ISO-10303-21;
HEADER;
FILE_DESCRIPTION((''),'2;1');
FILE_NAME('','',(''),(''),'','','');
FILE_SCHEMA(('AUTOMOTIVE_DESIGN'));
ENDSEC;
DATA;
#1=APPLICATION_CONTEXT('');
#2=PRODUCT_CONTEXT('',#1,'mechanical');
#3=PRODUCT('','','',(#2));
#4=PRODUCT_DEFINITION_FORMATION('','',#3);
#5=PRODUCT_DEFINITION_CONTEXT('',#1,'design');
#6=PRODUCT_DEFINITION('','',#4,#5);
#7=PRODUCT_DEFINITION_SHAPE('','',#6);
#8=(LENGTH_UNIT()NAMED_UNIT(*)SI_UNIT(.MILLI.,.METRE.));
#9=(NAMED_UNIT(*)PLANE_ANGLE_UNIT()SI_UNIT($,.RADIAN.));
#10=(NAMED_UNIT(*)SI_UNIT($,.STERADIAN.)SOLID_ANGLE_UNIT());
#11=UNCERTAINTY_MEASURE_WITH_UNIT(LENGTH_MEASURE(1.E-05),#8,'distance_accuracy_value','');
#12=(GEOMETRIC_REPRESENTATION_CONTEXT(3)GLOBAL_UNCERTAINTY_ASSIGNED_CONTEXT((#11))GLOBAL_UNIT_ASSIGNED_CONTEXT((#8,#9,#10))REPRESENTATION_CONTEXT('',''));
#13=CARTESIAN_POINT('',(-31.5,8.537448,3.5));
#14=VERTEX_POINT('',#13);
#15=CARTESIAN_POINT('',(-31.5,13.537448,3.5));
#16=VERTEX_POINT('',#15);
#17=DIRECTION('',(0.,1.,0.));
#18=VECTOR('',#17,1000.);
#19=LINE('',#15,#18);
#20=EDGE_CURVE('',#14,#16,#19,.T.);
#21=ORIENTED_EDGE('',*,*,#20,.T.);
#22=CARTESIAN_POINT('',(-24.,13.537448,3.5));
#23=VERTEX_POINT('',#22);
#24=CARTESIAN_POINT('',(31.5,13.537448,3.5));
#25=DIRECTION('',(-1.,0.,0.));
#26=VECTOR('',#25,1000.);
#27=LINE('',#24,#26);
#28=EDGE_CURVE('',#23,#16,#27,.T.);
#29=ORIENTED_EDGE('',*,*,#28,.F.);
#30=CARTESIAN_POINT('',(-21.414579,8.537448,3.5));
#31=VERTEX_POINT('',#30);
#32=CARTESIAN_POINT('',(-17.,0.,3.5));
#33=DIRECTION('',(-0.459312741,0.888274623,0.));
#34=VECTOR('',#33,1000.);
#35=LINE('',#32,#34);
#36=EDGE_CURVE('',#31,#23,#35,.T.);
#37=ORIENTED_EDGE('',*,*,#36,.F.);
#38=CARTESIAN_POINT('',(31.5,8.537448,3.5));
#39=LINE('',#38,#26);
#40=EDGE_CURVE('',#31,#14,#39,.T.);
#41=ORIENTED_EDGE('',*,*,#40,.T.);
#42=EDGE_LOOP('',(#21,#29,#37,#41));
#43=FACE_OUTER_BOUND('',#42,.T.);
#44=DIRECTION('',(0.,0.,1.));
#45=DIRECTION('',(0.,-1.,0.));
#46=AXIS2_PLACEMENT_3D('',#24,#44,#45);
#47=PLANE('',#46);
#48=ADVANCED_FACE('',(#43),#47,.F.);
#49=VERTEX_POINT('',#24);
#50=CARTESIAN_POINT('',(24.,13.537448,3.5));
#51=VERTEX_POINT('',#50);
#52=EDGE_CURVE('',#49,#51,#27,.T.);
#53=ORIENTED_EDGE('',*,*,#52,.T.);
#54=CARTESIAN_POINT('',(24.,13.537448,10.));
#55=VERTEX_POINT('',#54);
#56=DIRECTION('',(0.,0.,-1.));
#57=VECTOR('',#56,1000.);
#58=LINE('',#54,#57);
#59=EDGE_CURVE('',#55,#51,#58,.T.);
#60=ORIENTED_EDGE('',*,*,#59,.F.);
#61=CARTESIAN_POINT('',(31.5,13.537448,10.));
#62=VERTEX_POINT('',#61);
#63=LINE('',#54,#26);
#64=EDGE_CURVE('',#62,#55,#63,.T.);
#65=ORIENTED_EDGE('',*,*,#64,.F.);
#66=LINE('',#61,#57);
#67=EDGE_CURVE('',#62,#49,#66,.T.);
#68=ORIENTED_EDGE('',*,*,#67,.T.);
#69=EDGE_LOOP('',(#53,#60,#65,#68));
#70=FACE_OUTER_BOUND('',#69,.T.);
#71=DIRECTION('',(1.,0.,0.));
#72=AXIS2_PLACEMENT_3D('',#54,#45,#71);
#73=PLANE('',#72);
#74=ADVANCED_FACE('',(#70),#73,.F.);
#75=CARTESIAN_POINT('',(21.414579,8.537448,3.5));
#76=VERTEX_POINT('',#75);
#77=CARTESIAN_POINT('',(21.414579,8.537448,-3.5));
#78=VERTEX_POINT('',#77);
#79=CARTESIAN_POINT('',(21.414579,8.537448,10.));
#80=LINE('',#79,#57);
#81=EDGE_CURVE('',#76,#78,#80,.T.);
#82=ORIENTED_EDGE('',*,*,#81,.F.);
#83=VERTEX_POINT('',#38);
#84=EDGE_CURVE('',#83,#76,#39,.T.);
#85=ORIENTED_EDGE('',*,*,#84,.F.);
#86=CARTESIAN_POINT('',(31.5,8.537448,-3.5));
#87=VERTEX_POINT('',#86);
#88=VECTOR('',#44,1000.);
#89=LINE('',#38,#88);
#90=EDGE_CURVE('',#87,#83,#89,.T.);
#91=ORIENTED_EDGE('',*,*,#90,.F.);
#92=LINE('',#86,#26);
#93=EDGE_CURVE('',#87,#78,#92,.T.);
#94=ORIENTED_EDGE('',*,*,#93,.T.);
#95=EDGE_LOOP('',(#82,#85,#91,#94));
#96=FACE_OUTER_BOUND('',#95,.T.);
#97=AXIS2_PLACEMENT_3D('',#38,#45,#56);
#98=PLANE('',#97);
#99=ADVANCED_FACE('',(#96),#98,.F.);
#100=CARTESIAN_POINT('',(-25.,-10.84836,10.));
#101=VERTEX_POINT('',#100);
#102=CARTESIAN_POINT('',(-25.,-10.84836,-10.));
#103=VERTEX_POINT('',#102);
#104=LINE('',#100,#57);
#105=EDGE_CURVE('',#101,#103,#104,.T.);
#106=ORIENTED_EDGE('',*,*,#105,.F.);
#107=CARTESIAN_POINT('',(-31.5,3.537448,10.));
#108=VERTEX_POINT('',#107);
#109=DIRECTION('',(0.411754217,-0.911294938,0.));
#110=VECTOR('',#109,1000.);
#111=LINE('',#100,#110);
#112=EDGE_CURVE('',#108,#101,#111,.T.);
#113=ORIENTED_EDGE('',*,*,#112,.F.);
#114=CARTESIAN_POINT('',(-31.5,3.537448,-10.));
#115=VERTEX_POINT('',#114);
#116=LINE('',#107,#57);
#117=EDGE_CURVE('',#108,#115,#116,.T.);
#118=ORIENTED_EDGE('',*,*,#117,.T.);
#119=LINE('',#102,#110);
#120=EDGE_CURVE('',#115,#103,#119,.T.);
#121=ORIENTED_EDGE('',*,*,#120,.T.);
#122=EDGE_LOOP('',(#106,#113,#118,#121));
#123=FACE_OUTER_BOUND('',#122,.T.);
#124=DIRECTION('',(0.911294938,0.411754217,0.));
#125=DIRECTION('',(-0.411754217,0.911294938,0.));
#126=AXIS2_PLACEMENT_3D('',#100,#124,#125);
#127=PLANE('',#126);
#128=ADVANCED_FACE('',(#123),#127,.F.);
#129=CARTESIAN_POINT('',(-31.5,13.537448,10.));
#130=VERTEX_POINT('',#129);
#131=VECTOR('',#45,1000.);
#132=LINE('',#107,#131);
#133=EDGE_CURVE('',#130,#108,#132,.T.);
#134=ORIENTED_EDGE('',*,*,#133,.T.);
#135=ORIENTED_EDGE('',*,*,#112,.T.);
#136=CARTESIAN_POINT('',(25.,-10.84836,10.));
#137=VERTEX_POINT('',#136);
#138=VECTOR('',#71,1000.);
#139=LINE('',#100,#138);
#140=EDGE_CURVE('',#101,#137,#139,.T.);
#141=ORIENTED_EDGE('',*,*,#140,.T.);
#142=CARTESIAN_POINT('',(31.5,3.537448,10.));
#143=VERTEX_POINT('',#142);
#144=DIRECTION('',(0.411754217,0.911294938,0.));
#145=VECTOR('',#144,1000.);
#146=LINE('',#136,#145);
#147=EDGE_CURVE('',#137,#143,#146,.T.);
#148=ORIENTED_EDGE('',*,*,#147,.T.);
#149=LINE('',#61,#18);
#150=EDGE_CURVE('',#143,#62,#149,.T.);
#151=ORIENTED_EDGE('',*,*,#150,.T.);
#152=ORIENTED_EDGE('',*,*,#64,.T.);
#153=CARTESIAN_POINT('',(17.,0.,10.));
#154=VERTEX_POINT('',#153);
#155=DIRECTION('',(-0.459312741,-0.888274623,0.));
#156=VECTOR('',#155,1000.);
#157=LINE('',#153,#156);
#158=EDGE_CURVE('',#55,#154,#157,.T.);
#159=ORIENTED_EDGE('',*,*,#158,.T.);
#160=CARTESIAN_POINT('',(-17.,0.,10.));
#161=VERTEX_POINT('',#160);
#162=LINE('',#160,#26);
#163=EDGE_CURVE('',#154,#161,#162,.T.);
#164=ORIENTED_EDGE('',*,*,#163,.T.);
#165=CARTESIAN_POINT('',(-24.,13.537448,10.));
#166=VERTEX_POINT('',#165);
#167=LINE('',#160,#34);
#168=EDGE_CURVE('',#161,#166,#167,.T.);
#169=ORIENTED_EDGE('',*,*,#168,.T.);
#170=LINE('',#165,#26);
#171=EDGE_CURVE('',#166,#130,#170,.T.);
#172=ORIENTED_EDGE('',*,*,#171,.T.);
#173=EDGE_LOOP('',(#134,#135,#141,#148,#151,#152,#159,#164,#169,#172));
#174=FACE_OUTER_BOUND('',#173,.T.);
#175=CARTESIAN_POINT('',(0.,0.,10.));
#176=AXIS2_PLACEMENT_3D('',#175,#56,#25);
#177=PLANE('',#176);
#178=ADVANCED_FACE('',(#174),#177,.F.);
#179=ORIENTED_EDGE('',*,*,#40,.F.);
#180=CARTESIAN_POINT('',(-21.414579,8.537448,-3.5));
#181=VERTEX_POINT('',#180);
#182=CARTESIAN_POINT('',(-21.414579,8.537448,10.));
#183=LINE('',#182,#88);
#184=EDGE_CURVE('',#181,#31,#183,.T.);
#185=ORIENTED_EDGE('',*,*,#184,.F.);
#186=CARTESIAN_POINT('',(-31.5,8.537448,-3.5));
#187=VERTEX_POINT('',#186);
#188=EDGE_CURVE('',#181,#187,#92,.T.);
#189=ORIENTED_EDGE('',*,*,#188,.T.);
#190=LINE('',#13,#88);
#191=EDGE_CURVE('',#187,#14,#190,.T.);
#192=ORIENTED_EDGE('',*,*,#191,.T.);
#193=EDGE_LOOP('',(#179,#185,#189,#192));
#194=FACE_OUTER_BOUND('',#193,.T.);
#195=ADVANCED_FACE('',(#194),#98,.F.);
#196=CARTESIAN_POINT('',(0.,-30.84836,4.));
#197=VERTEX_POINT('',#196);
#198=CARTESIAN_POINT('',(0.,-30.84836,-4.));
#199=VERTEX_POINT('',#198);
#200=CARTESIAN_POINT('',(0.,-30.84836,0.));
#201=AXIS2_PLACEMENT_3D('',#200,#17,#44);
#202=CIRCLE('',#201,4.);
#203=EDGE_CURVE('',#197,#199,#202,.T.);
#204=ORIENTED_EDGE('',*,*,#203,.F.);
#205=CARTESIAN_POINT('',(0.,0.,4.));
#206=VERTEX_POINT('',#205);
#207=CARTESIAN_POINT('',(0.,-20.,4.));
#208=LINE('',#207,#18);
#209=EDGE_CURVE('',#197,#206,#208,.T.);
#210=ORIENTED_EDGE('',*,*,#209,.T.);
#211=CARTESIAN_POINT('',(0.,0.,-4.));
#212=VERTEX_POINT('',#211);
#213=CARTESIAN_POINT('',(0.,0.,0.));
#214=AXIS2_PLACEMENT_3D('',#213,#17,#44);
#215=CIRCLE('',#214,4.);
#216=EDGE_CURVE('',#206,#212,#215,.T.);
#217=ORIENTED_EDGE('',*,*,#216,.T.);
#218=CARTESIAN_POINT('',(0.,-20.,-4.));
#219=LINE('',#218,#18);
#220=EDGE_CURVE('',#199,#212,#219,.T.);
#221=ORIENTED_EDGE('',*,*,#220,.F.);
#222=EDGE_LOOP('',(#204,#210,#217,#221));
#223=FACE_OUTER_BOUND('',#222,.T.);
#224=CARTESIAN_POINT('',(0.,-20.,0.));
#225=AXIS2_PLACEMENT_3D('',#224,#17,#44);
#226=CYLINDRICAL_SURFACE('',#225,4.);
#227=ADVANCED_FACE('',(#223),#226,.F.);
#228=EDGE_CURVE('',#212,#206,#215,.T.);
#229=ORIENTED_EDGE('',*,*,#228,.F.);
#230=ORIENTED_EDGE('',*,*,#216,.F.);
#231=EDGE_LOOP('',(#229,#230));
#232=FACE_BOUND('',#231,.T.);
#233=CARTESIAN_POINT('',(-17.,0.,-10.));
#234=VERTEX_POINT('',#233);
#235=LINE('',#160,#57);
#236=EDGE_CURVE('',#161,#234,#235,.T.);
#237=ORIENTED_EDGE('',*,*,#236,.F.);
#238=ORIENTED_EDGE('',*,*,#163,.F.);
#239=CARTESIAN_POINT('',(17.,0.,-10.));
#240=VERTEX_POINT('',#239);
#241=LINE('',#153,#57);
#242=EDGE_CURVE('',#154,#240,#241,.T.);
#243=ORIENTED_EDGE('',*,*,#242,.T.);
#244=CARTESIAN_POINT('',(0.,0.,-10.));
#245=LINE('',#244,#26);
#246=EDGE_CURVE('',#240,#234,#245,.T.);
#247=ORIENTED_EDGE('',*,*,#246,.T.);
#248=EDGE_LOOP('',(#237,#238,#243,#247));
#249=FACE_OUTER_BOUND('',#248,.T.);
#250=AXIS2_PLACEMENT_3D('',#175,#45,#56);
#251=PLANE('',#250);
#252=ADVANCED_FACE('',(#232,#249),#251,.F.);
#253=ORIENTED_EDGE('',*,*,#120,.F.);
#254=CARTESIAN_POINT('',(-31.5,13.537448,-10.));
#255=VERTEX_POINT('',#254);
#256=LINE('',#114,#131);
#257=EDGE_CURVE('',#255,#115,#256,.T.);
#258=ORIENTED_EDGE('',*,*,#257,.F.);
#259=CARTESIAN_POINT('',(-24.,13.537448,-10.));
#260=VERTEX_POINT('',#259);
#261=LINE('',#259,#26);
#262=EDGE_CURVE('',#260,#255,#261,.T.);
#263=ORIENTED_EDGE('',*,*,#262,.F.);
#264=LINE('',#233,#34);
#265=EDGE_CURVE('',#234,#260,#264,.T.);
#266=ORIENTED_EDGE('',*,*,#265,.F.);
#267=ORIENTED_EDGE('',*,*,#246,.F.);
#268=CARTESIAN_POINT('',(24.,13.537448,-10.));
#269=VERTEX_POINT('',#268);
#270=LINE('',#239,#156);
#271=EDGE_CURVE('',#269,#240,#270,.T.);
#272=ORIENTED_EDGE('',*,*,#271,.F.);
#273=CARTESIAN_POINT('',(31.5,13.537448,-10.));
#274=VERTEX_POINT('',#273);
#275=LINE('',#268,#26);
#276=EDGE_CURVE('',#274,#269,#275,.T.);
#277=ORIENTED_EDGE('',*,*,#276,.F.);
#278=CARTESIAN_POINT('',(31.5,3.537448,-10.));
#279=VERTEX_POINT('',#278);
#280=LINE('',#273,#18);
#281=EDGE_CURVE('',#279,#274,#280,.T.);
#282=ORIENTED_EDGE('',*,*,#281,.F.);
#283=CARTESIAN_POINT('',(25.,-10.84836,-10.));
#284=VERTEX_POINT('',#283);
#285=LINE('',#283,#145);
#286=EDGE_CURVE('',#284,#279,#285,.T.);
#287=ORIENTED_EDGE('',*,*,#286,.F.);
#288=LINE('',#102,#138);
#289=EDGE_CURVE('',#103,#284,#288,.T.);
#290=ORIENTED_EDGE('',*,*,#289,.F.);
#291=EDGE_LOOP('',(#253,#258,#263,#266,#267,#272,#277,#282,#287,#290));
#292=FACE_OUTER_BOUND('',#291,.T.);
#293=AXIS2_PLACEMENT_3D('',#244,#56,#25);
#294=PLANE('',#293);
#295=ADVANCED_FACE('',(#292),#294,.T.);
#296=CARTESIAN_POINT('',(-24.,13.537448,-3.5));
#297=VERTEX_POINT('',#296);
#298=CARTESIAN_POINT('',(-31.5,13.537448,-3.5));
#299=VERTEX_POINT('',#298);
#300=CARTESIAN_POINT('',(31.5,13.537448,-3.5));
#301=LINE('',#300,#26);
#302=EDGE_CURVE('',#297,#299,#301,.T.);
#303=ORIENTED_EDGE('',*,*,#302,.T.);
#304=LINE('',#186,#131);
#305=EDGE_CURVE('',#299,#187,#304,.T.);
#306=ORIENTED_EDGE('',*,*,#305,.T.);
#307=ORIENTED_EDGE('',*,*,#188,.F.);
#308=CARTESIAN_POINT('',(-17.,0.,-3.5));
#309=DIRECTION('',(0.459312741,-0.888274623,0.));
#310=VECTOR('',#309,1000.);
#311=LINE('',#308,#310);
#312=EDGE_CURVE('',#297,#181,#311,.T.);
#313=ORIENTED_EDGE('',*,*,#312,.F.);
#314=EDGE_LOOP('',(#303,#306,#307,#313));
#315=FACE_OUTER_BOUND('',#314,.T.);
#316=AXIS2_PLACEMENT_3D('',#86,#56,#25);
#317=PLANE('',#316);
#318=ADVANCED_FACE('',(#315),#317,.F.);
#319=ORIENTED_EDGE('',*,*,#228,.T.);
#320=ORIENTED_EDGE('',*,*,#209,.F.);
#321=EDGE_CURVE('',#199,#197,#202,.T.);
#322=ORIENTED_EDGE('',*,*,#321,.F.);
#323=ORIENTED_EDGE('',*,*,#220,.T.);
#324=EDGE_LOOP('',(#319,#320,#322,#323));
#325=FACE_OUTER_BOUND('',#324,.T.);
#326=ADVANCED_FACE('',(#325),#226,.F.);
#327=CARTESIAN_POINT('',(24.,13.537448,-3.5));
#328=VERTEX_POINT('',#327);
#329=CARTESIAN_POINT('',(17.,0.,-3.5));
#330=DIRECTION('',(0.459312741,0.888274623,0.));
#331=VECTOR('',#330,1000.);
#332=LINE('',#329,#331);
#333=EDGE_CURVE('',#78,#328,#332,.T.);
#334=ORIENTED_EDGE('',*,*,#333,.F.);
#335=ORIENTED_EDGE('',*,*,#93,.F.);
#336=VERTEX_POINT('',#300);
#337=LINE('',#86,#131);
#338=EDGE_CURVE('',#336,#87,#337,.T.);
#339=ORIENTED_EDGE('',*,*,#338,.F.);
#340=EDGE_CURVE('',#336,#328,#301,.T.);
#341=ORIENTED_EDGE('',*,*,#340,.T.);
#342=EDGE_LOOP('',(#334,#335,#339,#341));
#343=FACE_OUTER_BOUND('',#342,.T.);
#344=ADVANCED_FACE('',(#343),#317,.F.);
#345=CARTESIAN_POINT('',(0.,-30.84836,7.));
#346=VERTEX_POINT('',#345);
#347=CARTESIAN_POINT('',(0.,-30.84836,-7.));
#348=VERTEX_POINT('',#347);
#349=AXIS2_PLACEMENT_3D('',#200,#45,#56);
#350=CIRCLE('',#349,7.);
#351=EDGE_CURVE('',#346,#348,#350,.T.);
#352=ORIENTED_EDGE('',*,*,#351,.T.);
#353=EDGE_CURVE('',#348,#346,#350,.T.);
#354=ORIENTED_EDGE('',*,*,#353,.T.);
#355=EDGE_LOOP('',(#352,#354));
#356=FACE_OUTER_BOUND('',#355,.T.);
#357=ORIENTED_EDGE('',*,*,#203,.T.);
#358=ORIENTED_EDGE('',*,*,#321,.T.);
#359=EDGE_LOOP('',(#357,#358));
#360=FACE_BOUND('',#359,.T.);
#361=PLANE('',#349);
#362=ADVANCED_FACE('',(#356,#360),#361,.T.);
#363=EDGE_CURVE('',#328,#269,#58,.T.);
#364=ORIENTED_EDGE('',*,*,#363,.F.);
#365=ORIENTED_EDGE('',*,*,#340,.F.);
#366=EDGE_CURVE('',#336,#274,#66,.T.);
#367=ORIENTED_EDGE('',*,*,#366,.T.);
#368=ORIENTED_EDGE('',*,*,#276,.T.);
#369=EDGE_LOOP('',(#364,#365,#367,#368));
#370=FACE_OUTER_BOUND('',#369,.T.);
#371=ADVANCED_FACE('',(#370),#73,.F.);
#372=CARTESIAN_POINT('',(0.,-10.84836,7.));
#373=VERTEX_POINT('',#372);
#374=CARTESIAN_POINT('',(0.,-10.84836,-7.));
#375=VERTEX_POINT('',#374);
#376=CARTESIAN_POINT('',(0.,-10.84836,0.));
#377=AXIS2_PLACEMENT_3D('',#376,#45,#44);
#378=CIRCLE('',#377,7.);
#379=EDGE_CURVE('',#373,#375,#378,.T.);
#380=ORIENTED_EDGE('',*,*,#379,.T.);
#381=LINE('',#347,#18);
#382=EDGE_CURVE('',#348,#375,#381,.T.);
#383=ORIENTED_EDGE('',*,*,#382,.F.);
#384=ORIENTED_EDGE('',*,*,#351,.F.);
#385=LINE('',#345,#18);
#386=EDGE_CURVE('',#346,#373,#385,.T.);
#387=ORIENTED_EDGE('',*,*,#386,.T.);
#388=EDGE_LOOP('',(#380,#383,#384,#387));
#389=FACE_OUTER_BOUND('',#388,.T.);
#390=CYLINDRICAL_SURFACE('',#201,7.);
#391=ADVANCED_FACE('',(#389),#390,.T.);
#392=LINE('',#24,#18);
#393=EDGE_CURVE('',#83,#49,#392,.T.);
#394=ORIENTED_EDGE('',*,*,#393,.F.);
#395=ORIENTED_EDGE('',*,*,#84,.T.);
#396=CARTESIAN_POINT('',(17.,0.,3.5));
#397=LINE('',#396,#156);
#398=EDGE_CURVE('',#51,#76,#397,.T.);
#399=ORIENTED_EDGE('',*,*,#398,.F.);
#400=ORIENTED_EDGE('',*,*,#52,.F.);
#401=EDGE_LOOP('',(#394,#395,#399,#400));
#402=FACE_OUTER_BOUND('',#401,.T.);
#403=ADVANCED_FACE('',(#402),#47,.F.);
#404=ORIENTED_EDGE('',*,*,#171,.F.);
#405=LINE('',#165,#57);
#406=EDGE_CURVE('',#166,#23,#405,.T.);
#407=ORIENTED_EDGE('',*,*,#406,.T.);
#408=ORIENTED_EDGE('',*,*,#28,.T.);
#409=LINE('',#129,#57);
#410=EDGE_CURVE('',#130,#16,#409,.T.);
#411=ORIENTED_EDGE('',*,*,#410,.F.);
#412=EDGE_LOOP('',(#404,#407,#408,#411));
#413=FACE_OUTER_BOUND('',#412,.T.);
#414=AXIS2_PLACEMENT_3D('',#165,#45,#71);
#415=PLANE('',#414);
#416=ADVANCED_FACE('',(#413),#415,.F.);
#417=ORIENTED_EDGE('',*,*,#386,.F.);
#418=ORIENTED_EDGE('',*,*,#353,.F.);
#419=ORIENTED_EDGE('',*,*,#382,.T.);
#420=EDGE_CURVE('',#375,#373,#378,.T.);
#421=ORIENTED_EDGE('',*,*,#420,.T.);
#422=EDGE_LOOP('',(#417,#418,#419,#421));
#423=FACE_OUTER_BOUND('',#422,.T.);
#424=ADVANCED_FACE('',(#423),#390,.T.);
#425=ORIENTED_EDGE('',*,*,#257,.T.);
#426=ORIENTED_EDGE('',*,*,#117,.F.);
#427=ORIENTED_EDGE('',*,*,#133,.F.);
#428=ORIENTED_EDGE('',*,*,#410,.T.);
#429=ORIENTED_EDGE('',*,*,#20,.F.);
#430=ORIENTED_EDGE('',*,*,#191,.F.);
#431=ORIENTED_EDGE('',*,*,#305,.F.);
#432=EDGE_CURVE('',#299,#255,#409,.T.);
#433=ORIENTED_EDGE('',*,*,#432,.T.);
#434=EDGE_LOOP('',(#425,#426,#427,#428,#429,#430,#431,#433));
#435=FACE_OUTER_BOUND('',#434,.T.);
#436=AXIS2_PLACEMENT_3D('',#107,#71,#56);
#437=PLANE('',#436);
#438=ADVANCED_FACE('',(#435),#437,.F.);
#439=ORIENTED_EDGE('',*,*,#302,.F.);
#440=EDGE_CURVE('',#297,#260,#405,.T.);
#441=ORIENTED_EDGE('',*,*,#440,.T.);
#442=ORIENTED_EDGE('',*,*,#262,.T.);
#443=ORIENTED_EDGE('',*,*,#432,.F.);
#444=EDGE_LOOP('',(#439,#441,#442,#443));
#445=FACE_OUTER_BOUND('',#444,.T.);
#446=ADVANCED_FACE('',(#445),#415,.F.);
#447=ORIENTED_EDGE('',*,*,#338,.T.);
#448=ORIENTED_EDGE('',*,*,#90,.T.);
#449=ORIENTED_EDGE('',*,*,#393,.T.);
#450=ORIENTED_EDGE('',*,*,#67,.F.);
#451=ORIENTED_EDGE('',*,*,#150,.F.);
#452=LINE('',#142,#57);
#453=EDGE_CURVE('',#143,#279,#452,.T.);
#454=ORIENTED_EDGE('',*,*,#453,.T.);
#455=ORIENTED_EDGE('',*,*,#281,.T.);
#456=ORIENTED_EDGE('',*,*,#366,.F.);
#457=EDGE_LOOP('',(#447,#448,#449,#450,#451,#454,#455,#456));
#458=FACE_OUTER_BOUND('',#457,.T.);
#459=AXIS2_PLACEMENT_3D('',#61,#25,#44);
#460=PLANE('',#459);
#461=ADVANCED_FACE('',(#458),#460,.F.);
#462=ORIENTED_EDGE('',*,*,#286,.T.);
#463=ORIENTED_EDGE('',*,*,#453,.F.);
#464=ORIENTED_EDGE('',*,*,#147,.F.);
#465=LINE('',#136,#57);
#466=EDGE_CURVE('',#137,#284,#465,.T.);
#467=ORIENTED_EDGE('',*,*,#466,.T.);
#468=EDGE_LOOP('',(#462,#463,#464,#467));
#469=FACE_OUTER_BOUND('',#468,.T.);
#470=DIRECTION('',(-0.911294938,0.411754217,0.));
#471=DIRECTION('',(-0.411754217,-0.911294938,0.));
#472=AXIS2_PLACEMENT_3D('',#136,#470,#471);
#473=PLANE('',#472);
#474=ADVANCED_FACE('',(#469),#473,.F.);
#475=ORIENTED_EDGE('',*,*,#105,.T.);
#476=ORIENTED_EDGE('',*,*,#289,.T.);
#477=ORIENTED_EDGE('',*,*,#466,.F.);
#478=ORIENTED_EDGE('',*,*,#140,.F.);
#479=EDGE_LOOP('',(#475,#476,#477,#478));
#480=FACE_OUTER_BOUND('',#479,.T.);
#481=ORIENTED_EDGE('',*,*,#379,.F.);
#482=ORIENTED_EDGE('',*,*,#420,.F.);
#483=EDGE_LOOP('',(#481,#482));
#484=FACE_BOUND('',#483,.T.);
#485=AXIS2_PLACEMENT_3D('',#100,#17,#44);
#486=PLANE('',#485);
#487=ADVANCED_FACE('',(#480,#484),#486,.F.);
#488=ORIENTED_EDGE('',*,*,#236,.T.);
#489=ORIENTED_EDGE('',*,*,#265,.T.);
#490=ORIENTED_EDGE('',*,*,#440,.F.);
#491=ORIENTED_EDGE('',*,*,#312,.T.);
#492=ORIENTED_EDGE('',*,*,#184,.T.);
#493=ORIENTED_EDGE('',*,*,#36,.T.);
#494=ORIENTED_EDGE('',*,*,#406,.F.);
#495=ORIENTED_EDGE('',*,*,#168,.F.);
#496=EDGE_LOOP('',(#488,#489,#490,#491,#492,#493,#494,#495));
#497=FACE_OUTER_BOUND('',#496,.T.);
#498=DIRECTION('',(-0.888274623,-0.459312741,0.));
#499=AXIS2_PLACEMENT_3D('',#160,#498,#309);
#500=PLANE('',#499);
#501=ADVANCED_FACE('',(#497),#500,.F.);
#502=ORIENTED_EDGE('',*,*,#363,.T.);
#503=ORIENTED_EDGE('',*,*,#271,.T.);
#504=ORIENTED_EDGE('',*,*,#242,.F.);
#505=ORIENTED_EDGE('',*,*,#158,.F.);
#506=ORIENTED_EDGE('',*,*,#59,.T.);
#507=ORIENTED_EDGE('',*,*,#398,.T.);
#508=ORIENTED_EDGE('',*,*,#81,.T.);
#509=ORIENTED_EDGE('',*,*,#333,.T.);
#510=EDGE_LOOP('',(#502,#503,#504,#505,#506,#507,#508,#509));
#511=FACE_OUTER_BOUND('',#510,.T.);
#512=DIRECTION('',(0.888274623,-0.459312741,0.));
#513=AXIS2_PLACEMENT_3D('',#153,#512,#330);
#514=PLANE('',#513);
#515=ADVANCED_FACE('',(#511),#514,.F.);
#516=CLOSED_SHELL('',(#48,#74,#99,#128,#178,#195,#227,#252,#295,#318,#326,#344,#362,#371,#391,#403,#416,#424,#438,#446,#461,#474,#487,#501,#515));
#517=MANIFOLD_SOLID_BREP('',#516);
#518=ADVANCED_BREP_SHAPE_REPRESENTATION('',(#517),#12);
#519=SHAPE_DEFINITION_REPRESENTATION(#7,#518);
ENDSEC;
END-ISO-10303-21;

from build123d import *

# Parameters (mm, degrees)
YOKE_BODY_DEPTH      = 10
ARM_SLOTS_DEPTH      = 66.209374322
POST_SEAT_SKETCH_R   = 4
POST_SEAT_CUT_DEPTH  = 20
PIVOT_POST_SKETCH_R  = 7
PIVOT_POST_DEPTH     = 20
CENTRE_HOLE_SKETCH_R = 4
CENTRE_HOLE_DEPTH    = 46.209194984


with BuildPart() as part:
    # Yoke Profile Sketch → Yoke Body (new, symmetric)
    with BuildSketch(Plane.XY):
        Polygon((0, 0), (17, 0), (24, 13.537448042), (31.5, 13.537448042), (31.5, 3.537448042), (25, -10.848359941), (-25, -10.848359941), (-31.5, 3.537448042), (-31.5, 13.537448042), (-24, 13.537448042), (-17, 0), align=None)
    extrude(amount=YOKE_BODY_DEPTH, both=True)

    # Arm Slots Sketch → Arm Slots (cut, through all)
    with BuildSketch(Plane.ZY.offset(31.5)):
        Polygon((0, 13.537448042), (3.5, 13.537448042), (3.5, 8.537448042), (-3.5, 8.537448042), (-3.5, 13.537448042), align=None)
    extrude(amount=-ARM_SLOTS_DEPTH, mode=Mode.SUBTRACT)

    # Post Seat Sketch → Post Seat Cut (cut)
    with BuildSketch(Plane(origin=(0, 0, 0), x_dir=(1, 0, 0), z_dir=(0, 1, 0))):
        with Locations(Location((0, 0, 0), (0, 0, 270))):
            Circle(POST_SEAT_SKETCH_R)
    extrude(amount=-POST_SEAT_CUT_DEPTH, mode=Mode.SUBTRACT)

    # Pivot Post Sketch → Pivot Post (add)
    with BuildSketch(Plane.XZ.offset(10.848359941)):
        with Locations(Location((0, 0, 0), (0, 0, 90))):
            Circle(PIVOT_POST_SKETCH_R)
    extrude(amount=PIVOT_POST_DEPTH)

    # Centre Hole Sketch → Centre Hole (cut, through all)
    with BuildSketch(Plane(origin=(0, 0, 0), x_dir=(1, 0, 0), z_dir=(0, 1, 0))):
        with Locations(Location((0, 0, 0), (0, 0, 270))):
            Circle(CENTRE_HOLE_SKETCH_R)
    extrude(amount=-CENTRE_HOLE_DEPTH, mode=Mode.SUBTRACT)


solid = part.part
